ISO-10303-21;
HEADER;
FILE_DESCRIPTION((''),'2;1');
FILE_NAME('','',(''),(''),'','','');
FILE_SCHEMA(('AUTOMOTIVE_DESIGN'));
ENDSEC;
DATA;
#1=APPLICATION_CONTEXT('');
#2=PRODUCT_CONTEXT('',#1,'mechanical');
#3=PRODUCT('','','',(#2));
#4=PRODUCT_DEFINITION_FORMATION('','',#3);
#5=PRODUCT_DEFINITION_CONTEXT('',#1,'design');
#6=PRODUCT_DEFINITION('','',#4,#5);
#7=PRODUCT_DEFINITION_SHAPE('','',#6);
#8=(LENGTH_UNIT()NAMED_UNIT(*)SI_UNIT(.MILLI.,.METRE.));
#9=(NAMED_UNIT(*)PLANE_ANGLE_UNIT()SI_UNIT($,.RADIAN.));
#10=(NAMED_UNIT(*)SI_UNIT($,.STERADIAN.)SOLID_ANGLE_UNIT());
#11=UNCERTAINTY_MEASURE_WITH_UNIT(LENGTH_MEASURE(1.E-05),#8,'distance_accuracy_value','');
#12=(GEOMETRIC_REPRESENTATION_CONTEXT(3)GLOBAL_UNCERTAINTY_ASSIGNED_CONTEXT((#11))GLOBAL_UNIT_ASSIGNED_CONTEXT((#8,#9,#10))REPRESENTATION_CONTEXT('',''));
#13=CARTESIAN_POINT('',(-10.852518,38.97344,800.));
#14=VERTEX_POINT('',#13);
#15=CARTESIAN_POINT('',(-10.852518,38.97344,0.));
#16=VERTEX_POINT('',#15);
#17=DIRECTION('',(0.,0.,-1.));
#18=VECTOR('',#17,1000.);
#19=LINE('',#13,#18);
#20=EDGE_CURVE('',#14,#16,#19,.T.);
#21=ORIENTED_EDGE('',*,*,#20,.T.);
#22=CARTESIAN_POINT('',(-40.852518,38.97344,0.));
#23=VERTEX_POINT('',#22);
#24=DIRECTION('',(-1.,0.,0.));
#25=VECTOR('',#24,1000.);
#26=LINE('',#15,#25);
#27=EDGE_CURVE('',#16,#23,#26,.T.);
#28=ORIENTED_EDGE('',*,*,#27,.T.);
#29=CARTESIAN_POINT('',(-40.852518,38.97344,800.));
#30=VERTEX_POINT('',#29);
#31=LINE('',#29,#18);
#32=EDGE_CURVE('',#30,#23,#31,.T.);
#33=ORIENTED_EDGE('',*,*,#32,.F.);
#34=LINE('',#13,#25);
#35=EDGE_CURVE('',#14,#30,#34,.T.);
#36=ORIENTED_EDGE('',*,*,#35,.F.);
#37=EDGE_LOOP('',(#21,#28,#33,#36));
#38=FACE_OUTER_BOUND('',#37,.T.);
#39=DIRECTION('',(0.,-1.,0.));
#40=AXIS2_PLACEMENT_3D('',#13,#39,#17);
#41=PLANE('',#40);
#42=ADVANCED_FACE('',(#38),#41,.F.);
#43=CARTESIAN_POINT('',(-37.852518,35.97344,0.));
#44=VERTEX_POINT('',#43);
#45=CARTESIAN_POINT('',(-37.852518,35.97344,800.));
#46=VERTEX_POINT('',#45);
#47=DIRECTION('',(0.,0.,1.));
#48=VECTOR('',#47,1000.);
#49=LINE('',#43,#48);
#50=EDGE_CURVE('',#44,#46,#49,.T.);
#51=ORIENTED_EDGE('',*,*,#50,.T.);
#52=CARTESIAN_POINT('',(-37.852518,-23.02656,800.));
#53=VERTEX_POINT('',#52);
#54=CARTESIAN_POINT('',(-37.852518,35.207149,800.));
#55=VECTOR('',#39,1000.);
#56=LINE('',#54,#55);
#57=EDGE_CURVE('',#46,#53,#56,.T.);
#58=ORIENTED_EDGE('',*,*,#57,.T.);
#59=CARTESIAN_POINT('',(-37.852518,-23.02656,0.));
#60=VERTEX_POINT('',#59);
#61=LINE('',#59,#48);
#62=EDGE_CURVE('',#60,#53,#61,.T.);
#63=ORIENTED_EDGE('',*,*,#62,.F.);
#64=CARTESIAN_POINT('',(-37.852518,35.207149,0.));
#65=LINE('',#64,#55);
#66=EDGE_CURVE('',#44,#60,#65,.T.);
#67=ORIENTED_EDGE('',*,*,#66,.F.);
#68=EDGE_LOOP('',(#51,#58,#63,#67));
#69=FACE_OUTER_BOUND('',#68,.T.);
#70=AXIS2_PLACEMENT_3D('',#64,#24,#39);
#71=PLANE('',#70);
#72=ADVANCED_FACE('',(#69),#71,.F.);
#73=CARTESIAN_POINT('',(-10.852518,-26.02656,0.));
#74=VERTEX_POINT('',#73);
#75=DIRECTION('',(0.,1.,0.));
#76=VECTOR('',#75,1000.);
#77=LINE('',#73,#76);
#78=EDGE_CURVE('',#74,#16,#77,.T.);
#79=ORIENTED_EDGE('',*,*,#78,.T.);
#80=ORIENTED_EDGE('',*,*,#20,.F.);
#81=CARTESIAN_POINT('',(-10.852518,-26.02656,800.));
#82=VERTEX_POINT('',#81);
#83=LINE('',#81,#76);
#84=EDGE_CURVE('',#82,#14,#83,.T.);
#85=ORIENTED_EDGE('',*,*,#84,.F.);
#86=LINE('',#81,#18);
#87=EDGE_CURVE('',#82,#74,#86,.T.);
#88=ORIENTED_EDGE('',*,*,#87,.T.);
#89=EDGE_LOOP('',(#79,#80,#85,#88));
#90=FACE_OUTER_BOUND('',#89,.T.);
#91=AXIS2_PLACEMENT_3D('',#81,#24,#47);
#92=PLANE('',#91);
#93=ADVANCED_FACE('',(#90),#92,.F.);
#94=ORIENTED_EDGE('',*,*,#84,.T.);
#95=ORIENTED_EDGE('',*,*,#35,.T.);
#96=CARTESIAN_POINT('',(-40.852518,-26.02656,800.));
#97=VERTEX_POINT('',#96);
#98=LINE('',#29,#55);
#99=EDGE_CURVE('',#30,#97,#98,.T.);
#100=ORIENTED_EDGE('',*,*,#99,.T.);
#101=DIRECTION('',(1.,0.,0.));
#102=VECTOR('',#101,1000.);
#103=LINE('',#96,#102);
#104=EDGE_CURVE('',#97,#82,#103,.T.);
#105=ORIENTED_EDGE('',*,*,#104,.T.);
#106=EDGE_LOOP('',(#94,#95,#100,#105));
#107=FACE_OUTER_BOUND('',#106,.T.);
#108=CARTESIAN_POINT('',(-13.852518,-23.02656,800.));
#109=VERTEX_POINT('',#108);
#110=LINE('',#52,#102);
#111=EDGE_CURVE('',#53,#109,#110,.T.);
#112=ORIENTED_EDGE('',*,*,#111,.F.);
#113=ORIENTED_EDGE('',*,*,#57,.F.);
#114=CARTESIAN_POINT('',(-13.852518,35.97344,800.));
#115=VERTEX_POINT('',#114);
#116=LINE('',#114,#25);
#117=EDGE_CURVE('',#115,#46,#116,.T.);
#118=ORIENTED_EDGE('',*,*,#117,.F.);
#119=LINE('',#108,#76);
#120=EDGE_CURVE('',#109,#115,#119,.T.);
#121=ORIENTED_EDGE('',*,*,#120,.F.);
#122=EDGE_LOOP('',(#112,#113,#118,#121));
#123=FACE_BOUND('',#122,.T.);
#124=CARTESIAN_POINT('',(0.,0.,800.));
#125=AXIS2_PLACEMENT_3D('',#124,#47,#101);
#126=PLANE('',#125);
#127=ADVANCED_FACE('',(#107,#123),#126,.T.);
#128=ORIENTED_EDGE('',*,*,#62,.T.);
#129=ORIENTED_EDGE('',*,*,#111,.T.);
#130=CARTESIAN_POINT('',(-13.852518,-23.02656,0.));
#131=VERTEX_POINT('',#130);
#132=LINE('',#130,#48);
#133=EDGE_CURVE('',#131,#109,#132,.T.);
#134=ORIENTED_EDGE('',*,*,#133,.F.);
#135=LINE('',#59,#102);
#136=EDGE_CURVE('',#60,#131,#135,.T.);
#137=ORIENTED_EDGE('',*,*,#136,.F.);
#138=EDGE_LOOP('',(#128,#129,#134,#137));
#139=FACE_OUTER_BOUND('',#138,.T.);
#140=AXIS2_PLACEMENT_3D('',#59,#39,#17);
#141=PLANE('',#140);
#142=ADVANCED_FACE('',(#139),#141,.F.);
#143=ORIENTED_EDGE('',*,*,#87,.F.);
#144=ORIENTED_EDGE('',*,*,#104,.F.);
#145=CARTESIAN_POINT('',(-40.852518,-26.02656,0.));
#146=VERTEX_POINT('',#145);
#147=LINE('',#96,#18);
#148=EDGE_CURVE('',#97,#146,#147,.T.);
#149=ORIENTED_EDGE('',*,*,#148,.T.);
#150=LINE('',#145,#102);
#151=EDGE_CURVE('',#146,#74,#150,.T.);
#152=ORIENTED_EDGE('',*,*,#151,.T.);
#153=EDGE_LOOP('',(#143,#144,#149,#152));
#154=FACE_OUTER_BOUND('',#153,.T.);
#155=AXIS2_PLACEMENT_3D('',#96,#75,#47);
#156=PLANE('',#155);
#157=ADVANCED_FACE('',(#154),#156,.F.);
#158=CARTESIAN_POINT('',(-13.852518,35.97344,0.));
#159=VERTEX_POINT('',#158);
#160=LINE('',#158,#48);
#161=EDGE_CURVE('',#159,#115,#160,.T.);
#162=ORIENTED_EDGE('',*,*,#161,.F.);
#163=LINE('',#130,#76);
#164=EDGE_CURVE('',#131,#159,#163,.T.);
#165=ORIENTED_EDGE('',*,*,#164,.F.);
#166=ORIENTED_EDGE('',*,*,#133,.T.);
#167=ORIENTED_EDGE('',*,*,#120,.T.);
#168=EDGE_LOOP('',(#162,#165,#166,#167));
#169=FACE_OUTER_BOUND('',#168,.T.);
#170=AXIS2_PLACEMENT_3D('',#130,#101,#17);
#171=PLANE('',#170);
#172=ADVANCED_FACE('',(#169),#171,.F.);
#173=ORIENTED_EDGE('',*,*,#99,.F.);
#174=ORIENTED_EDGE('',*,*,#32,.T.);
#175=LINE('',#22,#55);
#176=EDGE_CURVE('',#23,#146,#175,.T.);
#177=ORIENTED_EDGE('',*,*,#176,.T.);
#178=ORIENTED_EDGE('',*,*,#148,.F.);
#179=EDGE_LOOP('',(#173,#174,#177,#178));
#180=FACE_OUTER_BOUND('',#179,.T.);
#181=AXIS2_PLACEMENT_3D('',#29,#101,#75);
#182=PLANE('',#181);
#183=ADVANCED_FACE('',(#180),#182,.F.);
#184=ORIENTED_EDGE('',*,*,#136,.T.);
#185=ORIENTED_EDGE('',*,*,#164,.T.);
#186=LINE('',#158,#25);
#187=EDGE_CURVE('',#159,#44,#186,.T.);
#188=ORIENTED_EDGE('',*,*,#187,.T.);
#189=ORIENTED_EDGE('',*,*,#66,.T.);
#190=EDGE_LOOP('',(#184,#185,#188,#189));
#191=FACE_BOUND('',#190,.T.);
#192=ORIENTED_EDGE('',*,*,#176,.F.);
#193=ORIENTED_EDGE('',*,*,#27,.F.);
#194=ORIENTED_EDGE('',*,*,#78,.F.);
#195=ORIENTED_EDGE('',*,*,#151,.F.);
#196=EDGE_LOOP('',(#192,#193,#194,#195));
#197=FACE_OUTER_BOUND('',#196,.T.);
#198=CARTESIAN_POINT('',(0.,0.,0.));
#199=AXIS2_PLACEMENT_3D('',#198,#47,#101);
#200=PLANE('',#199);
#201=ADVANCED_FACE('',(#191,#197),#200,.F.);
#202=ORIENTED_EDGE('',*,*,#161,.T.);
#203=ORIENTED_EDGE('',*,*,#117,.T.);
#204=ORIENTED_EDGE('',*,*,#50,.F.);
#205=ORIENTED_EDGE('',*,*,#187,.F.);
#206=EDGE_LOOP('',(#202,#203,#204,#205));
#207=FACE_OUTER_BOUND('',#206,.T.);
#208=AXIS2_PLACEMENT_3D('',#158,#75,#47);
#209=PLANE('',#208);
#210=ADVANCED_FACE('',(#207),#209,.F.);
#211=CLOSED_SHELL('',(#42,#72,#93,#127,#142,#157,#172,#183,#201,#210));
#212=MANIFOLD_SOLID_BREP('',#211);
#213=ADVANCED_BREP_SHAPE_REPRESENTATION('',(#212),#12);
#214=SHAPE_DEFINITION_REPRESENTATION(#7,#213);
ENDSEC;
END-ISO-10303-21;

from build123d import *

# Parameters (mm, degrees)
SKETCH1_W           = 30
SKETCH1_H           = 65
BOSS_EXTRUDE1_DEPTH = 800
CUT_EXTRUDE1_DEPTH  = 800


with BuildPart() as part:
    # Sketch1 → Boss-Extrude1 (new body)
    with BuildSketch(Plane.XY):
        with Locations((-25.852518101, 6.473439942)):
            Rectangle(SKETCH1_W, SKETCH1_H)
    extrude(amount=BOSS_EXTRUDE1_DEPTH)

    # Sketch2 → Cut-Extrude1 (cut)
    with BuildSketch(Plane.XY.offset(800)):
        Polygon((-37.852518101, 35.207148711), (-37.852518101, -23.026560058), (-13.852518101, -23.026560058), (-13.852518101, 35.973439942), (-37.852518101, 35.973439942), align=None)
    extrude(amount=-CUT_EXTRUDE1_DEPTH, mode=Mode.SUBTRACT)


solid = part.part
